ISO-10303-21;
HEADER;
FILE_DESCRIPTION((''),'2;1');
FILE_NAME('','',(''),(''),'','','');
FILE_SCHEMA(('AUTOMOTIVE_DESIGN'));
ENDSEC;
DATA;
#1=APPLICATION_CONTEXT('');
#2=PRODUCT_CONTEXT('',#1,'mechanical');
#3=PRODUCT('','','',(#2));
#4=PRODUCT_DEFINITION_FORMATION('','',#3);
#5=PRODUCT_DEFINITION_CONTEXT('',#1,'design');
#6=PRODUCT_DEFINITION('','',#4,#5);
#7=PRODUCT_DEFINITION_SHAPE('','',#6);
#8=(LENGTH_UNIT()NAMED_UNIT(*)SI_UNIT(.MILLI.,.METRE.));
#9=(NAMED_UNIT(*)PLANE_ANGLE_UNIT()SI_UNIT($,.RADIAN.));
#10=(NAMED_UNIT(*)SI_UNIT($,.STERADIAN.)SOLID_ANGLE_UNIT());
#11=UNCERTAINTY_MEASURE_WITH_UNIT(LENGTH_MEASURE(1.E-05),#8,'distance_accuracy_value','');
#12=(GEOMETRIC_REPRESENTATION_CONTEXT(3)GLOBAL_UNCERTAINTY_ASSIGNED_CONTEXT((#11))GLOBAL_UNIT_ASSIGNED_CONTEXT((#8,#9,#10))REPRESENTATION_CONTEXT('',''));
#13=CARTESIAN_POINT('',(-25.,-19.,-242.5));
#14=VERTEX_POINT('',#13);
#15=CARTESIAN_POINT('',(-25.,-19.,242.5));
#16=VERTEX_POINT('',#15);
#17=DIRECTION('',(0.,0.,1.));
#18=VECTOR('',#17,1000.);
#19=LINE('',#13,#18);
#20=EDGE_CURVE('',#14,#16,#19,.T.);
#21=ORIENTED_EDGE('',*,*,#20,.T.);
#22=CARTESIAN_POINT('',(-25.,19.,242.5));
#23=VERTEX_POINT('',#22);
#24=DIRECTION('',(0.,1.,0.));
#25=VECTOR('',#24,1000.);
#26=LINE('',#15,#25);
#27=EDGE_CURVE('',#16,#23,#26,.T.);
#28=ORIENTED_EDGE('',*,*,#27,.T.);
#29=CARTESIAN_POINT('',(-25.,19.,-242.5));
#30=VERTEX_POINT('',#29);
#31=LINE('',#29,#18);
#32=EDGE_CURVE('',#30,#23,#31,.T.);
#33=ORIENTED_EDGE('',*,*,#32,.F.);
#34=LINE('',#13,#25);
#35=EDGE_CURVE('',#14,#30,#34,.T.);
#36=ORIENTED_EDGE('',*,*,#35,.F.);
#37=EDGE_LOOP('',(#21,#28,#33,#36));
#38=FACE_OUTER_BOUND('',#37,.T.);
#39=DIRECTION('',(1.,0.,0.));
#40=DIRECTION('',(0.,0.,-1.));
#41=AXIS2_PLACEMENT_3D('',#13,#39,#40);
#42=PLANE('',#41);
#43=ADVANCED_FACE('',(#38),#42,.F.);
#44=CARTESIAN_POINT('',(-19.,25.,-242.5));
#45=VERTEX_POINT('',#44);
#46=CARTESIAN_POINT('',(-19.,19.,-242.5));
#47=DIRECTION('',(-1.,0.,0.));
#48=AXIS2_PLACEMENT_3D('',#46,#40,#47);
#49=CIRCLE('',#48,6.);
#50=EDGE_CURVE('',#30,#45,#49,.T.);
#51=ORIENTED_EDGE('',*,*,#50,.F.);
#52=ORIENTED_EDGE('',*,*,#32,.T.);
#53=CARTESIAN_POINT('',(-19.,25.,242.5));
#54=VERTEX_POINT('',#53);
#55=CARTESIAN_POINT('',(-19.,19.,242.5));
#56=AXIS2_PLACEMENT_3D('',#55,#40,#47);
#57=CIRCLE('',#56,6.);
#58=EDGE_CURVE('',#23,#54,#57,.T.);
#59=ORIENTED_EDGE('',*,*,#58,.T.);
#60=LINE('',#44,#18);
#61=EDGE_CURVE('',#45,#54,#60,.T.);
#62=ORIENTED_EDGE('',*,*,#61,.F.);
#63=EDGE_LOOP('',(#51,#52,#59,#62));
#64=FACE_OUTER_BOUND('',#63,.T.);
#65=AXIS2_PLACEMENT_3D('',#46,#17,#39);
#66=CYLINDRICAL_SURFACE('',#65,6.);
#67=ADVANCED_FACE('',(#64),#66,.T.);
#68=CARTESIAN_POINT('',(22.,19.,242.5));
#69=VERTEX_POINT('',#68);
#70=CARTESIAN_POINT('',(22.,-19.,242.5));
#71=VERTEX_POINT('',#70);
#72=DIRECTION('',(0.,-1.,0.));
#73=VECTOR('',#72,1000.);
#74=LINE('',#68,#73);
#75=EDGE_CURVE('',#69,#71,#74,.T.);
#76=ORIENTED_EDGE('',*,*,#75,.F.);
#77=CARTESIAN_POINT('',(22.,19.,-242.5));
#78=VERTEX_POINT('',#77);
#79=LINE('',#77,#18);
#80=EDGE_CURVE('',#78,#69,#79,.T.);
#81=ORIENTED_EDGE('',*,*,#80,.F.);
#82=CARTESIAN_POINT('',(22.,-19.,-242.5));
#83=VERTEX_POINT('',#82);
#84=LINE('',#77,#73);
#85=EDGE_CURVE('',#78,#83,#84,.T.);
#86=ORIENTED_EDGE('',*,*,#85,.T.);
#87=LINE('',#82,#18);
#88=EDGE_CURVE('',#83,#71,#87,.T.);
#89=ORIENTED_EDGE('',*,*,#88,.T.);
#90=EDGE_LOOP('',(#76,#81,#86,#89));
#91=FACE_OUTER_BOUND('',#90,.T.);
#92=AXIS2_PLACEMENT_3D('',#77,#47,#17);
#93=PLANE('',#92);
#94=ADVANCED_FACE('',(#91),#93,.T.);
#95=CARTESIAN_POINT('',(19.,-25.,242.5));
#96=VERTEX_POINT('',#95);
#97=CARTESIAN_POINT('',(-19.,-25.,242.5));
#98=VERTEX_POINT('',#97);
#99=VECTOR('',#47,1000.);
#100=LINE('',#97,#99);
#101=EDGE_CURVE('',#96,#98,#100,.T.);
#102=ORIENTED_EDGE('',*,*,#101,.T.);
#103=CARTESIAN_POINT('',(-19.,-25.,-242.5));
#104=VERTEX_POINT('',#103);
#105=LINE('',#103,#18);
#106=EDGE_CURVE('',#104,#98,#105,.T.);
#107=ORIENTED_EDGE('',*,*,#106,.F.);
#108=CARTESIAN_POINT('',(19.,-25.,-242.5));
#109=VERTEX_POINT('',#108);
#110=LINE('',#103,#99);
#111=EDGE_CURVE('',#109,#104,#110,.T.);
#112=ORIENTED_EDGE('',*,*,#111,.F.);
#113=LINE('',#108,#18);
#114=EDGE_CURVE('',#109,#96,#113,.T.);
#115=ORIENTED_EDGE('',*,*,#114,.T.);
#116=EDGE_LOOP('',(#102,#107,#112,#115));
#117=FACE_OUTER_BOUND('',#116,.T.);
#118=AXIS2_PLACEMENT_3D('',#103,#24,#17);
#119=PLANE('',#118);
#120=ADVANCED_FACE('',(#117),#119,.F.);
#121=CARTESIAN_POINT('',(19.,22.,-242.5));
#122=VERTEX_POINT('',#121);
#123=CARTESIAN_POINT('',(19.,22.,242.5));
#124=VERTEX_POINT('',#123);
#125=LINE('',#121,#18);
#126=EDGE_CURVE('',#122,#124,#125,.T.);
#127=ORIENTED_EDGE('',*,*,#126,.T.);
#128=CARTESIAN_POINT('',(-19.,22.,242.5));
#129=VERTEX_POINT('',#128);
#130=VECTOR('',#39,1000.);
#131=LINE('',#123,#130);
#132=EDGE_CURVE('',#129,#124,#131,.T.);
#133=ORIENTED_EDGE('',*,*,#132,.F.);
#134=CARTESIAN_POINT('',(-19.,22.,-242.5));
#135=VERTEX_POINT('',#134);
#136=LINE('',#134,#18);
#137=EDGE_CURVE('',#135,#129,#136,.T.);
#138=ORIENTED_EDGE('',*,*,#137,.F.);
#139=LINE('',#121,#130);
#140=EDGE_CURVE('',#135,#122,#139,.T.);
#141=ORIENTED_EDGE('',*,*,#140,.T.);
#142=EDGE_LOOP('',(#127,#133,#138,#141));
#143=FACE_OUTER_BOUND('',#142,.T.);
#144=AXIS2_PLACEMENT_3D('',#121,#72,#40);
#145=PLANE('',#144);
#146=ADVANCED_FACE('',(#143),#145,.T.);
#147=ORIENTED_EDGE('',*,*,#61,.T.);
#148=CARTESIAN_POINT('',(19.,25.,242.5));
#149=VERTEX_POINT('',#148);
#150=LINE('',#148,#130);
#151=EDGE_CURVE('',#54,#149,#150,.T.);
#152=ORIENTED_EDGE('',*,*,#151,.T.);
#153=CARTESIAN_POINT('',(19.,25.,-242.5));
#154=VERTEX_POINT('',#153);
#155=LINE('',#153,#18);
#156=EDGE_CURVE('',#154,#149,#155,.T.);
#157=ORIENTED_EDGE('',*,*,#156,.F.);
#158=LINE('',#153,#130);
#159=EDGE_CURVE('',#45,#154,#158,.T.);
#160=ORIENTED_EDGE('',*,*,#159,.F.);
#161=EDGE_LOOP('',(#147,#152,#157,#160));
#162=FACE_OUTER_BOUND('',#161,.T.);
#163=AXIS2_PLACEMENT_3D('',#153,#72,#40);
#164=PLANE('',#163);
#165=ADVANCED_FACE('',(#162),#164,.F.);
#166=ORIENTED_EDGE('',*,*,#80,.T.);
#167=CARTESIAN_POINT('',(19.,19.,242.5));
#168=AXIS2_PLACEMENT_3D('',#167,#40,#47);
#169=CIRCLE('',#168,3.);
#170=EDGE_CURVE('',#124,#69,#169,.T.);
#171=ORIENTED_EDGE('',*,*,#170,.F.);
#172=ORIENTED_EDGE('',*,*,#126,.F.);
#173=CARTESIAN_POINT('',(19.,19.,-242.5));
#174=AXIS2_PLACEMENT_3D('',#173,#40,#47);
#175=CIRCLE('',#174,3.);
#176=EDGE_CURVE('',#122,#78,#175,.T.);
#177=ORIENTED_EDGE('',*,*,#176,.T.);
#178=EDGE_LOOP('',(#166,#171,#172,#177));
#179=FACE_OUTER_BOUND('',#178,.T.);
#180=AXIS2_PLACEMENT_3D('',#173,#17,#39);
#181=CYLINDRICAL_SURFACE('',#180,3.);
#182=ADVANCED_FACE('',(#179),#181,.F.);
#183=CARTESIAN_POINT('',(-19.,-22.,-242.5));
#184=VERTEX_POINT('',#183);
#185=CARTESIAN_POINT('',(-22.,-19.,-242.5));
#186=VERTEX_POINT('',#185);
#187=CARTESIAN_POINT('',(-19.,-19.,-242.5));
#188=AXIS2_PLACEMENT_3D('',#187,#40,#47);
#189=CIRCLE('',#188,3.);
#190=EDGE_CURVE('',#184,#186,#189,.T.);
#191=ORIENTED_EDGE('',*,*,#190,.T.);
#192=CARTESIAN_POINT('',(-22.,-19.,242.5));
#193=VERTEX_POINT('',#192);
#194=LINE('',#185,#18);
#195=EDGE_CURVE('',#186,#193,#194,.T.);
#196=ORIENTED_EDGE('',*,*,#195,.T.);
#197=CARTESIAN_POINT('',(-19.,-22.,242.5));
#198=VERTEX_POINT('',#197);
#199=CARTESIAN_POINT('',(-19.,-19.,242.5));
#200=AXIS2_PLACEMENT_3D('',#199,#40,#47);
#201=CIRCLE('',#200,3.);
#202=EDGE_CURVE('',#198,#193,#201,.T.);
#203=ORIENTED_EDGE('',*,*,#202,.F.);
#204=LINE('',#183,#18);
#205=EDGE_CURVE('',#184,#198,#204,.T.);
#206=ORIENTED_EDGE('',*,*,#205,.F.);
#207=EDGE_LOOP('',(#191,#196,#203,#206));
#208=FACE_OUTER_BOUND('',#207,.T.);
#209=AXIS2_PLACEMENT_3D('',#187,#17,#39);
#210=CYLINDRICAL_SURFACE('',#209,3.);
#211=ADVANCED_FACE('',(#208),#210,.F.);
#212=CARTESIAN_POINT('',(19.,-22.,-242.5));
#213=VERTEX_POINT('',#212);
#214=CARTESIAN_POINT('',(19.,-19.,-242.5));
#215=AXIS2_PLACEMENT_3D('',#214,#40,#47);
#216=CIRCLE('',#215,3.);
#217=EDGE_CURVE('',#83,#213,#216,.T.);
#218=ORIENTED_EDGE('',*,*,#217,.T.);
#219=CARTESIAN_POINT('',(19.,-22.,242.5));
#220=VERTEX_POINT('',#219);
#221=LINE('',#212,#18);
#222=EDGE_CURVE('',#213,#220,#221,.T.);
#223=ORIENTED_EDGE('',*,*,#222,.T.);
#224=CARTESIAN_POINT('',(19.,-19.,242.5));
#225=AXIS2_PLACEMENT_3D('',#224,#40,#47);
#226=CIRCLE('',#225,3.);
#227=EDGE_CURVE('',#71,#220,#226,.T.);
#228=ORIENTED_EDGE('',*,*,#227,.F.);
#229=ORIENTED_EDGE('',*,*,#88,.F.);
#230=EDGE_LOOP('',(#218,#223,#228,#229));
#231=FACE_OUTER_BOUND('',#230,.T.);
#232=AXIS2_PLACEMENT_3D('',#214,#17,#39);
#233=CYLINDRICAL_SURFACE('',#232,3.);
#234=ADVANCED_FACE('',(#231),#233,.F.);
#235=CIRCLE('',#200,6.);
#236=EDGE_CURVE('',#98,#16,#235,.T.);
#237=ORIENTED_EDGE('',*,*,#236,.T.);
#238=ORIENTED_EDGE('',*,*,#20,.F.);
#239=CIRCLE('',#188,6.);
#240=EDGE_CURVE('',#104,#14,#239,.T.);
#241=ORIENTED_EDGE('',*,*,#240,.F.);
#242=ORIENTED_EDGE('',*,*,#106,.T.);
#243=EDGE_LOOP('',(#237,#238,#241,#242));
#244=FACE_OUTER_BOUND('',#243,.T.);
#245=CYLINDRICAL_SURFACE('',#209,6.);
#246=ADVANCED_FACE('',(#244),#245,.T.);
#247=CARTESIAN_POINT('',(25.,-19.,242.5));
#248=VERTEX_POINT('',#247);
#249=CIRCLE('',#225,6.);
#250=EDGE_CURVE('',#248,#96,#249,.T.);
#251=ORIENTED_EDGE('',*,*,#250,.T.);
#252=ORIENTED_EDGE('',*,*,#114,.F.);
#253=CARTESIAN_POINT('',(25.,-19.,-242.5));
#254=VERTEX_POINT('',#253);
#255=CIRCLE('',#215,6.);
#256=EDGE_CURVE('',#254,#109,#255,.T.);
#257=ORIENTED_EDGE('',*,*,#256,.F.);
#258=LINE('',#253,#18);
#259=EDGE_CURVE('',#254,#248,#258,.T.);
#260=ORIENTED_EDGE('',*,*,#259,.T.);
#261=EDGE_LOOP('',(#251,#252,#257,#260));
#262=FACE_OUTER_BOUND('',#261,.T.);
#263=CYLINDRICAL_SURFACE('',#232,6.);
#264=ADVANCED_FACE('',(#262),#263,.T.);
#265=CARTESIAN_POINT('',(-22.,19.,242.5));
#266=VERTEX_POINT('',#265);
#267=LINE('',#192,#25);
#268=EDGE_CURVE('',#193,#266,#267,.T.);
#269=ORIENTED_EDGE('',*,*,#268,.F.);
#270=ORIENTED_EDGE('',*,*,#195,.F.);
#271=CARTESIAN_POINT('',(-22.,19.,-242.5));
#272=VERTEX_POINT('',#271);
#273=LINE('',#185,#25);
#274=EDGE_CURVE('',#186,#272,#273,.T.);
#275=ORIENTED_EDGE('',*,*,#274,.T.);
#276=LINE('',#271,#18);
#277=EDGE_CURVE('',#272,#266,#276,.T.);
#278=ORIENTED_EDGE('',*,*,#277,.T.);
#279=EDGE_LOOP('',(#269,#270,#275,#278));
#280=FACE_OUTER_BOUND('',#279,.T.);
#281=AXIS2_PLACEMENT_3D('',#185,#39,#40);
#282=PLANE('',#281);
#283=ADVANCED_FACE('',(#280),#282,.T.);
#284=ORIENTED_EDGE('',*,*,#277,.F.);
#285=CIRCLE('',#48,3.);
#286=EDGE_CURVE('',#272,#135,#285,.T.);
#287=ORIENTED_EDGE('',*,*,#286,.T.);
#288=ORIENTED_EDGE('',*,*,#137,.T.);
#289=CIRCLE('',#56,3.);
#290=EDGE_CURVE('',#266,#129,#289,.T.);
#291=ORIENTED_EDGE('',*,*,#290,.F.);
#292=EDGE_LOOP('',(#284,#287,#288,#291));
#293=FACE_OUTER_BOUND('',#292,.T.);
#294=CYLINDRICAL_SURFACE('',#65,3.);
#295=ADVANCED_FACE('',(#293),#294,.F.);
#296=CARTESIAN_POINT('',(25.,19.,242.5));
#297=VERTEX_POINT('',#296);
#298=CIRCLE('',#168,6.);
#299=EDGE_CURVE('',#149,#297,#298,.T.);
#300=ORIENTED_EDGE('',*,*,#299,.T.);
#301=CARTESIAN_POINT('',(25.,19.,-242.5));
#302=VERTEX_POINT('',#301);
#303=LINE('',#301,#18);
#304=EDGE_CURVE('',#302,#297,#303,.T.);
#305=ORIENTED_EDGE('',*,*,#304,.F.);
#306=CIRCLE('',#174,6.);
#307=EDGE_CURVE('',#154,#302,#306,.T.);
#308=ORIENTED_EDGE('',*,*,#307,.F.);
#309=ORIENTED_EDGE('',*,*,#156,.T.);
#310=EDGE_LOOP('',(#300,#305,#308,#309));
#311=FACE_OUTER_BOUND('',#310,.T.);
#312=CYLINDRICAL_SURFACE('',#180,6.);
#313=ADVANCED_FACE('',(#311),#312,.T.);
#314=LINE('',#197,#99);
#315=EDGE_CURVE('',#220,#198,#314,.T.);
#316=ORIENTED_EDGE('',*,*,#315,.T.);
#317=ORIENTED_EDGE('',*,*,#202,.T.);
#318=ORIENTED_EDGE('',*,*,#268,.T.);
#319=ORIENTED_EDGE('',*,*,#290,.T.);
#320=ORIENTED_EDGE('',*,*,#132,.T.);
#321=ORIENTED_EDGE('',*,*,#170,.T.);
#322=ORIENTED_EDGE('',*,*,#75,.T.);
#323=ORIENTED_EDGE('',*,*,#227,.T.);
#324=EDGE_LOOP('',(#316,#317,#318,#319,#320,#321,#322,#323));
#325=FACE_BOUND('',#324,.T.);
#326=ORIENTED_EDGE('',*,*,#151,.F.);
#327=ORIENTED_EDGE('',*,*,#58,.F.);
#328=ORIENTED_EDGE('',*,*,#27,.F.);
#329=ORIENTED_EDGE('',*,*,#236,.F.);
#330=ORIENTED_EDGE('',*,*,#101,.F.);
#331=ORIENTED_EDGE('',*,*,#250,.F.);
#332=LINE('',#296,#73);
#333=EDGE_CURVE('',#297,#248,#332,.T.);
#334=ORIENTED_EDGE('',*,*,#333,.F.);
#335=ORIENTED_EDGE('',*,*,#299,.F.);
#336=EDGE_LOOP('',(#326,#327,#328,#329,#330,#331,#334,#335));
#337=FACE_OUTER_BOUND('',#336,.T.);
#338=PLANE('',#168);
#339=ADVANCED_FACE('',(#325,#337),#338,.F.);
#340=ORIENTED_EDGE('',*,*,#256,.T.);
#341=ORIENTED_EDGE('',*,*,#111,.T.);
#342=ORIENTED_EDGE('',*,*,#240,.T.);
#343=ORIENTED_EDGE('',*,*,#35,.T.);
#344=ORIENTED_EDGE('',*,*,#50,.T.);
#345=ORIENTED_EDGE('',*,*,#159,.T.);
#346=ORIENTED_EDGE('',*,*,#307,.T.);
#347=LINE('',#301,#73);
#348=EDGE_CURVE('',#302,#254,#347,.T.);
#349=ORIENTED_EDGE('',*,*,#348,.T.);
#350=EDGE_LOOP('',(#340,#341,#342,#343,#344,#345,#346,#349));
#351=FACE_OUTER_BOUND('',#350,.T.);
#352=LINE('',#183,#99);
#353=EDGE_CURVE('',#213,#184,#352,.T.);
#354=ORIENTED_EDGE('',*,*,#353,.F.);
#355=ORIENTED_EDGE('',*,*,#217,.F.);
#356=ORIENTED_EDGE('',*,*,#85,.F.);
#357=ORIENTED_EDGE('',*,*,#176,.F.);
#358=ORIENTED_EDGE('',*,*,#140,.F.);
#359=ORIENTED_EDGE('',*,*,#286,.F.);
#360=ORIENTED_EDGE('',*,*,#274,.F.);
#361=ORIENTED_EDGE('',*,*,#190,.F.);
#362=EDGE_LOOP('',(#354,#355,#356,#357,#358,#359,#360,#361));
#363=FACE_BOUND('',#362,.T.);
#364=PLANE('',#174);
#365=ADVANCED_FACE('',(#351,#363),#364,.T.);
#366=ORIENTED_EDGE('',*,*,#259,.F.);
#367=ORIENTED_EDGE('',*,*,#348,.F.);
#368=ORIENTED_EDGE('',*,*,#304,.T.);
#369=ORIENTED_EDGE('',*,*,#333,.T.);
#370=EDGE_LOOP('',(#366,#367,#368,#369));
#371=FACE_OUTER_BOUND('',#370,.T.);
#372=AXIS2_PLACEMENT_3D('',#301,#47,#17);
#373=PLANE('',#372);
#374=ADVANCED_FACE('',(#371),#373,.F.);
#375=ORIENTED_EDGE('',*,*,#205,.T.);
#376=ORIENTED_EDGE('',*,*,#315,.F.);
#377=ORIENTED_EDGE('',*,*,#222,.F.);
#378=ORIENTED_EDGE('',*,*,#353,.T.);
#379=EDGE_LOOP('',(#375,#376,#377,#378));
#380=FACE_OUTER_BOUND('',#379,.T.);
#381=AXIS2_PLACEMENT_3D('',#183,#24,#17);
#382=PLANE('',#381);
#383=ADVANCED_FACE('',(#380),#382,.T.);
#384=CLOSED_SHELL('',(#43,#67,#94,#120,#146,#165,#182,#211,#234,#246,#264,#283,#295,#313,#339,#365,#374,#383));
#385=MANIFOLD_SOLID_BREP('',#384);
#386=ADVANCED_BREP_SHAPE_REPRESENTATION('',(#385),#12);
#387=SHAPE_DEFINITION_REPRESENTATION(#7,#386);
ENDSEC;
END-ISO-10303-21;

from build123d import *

# Parameters (mm, degrees)
GB_6728_1986_050_X_50_X_3_1_DEPTH = 485


with BuildPart() as part:
    # Sketch1 → Gb／6728-1986方形空心型钢 050 X 50 X 3(1) (new body)
    with BuildSketch(Plane.YX.offset(-242.5)):
        with BuildLine():
            Line((-19, -25), (19, -25))
            ThreePointArc((19, -25), (23.242640687, -23.242640687), (25, -19))
            Line((25, -19), (25, 19))
            ThreePointArc((25, 19), (23.242640687, 23.242640687), (19, 25))
            Line((19, 25), (-19, 25))
            ThreePointArc((-19, 25), (-23.242640687, 23.242640687), (-25, 19))
            Line((-25, 19), (-25, -19))
            ThreePointArc((-25, -19), (-23.242640687, -23.242640687), (-19, -25))
        make_face()
        with BuildLine():
            Line((-19, -22), (19, -22))
            ThreePointArc((19, -22), (21.121320344, -21.121320344), (22, -19))
            Line((22, -19), (22, 19))
            ThreePointArc((22, 19), (21.121320344, 21.121320344), (19, 22))
            Line((19, 22), (-19, 22))
            ThreePointArc((-19, 22), (-21.121320344, 21.121320344), (-22, 19))
            Line((-22, 19), (-22, -19))
            ThreePointArc((-22, -19), (-21.121320344, -21.121320344), (-19, -22))
        make_face(mode=Mode.SUBTRACT)
    extrude(amount=GB_6728_1986_050_X_50_X_3_1_DEPTH)


solid = part.part
